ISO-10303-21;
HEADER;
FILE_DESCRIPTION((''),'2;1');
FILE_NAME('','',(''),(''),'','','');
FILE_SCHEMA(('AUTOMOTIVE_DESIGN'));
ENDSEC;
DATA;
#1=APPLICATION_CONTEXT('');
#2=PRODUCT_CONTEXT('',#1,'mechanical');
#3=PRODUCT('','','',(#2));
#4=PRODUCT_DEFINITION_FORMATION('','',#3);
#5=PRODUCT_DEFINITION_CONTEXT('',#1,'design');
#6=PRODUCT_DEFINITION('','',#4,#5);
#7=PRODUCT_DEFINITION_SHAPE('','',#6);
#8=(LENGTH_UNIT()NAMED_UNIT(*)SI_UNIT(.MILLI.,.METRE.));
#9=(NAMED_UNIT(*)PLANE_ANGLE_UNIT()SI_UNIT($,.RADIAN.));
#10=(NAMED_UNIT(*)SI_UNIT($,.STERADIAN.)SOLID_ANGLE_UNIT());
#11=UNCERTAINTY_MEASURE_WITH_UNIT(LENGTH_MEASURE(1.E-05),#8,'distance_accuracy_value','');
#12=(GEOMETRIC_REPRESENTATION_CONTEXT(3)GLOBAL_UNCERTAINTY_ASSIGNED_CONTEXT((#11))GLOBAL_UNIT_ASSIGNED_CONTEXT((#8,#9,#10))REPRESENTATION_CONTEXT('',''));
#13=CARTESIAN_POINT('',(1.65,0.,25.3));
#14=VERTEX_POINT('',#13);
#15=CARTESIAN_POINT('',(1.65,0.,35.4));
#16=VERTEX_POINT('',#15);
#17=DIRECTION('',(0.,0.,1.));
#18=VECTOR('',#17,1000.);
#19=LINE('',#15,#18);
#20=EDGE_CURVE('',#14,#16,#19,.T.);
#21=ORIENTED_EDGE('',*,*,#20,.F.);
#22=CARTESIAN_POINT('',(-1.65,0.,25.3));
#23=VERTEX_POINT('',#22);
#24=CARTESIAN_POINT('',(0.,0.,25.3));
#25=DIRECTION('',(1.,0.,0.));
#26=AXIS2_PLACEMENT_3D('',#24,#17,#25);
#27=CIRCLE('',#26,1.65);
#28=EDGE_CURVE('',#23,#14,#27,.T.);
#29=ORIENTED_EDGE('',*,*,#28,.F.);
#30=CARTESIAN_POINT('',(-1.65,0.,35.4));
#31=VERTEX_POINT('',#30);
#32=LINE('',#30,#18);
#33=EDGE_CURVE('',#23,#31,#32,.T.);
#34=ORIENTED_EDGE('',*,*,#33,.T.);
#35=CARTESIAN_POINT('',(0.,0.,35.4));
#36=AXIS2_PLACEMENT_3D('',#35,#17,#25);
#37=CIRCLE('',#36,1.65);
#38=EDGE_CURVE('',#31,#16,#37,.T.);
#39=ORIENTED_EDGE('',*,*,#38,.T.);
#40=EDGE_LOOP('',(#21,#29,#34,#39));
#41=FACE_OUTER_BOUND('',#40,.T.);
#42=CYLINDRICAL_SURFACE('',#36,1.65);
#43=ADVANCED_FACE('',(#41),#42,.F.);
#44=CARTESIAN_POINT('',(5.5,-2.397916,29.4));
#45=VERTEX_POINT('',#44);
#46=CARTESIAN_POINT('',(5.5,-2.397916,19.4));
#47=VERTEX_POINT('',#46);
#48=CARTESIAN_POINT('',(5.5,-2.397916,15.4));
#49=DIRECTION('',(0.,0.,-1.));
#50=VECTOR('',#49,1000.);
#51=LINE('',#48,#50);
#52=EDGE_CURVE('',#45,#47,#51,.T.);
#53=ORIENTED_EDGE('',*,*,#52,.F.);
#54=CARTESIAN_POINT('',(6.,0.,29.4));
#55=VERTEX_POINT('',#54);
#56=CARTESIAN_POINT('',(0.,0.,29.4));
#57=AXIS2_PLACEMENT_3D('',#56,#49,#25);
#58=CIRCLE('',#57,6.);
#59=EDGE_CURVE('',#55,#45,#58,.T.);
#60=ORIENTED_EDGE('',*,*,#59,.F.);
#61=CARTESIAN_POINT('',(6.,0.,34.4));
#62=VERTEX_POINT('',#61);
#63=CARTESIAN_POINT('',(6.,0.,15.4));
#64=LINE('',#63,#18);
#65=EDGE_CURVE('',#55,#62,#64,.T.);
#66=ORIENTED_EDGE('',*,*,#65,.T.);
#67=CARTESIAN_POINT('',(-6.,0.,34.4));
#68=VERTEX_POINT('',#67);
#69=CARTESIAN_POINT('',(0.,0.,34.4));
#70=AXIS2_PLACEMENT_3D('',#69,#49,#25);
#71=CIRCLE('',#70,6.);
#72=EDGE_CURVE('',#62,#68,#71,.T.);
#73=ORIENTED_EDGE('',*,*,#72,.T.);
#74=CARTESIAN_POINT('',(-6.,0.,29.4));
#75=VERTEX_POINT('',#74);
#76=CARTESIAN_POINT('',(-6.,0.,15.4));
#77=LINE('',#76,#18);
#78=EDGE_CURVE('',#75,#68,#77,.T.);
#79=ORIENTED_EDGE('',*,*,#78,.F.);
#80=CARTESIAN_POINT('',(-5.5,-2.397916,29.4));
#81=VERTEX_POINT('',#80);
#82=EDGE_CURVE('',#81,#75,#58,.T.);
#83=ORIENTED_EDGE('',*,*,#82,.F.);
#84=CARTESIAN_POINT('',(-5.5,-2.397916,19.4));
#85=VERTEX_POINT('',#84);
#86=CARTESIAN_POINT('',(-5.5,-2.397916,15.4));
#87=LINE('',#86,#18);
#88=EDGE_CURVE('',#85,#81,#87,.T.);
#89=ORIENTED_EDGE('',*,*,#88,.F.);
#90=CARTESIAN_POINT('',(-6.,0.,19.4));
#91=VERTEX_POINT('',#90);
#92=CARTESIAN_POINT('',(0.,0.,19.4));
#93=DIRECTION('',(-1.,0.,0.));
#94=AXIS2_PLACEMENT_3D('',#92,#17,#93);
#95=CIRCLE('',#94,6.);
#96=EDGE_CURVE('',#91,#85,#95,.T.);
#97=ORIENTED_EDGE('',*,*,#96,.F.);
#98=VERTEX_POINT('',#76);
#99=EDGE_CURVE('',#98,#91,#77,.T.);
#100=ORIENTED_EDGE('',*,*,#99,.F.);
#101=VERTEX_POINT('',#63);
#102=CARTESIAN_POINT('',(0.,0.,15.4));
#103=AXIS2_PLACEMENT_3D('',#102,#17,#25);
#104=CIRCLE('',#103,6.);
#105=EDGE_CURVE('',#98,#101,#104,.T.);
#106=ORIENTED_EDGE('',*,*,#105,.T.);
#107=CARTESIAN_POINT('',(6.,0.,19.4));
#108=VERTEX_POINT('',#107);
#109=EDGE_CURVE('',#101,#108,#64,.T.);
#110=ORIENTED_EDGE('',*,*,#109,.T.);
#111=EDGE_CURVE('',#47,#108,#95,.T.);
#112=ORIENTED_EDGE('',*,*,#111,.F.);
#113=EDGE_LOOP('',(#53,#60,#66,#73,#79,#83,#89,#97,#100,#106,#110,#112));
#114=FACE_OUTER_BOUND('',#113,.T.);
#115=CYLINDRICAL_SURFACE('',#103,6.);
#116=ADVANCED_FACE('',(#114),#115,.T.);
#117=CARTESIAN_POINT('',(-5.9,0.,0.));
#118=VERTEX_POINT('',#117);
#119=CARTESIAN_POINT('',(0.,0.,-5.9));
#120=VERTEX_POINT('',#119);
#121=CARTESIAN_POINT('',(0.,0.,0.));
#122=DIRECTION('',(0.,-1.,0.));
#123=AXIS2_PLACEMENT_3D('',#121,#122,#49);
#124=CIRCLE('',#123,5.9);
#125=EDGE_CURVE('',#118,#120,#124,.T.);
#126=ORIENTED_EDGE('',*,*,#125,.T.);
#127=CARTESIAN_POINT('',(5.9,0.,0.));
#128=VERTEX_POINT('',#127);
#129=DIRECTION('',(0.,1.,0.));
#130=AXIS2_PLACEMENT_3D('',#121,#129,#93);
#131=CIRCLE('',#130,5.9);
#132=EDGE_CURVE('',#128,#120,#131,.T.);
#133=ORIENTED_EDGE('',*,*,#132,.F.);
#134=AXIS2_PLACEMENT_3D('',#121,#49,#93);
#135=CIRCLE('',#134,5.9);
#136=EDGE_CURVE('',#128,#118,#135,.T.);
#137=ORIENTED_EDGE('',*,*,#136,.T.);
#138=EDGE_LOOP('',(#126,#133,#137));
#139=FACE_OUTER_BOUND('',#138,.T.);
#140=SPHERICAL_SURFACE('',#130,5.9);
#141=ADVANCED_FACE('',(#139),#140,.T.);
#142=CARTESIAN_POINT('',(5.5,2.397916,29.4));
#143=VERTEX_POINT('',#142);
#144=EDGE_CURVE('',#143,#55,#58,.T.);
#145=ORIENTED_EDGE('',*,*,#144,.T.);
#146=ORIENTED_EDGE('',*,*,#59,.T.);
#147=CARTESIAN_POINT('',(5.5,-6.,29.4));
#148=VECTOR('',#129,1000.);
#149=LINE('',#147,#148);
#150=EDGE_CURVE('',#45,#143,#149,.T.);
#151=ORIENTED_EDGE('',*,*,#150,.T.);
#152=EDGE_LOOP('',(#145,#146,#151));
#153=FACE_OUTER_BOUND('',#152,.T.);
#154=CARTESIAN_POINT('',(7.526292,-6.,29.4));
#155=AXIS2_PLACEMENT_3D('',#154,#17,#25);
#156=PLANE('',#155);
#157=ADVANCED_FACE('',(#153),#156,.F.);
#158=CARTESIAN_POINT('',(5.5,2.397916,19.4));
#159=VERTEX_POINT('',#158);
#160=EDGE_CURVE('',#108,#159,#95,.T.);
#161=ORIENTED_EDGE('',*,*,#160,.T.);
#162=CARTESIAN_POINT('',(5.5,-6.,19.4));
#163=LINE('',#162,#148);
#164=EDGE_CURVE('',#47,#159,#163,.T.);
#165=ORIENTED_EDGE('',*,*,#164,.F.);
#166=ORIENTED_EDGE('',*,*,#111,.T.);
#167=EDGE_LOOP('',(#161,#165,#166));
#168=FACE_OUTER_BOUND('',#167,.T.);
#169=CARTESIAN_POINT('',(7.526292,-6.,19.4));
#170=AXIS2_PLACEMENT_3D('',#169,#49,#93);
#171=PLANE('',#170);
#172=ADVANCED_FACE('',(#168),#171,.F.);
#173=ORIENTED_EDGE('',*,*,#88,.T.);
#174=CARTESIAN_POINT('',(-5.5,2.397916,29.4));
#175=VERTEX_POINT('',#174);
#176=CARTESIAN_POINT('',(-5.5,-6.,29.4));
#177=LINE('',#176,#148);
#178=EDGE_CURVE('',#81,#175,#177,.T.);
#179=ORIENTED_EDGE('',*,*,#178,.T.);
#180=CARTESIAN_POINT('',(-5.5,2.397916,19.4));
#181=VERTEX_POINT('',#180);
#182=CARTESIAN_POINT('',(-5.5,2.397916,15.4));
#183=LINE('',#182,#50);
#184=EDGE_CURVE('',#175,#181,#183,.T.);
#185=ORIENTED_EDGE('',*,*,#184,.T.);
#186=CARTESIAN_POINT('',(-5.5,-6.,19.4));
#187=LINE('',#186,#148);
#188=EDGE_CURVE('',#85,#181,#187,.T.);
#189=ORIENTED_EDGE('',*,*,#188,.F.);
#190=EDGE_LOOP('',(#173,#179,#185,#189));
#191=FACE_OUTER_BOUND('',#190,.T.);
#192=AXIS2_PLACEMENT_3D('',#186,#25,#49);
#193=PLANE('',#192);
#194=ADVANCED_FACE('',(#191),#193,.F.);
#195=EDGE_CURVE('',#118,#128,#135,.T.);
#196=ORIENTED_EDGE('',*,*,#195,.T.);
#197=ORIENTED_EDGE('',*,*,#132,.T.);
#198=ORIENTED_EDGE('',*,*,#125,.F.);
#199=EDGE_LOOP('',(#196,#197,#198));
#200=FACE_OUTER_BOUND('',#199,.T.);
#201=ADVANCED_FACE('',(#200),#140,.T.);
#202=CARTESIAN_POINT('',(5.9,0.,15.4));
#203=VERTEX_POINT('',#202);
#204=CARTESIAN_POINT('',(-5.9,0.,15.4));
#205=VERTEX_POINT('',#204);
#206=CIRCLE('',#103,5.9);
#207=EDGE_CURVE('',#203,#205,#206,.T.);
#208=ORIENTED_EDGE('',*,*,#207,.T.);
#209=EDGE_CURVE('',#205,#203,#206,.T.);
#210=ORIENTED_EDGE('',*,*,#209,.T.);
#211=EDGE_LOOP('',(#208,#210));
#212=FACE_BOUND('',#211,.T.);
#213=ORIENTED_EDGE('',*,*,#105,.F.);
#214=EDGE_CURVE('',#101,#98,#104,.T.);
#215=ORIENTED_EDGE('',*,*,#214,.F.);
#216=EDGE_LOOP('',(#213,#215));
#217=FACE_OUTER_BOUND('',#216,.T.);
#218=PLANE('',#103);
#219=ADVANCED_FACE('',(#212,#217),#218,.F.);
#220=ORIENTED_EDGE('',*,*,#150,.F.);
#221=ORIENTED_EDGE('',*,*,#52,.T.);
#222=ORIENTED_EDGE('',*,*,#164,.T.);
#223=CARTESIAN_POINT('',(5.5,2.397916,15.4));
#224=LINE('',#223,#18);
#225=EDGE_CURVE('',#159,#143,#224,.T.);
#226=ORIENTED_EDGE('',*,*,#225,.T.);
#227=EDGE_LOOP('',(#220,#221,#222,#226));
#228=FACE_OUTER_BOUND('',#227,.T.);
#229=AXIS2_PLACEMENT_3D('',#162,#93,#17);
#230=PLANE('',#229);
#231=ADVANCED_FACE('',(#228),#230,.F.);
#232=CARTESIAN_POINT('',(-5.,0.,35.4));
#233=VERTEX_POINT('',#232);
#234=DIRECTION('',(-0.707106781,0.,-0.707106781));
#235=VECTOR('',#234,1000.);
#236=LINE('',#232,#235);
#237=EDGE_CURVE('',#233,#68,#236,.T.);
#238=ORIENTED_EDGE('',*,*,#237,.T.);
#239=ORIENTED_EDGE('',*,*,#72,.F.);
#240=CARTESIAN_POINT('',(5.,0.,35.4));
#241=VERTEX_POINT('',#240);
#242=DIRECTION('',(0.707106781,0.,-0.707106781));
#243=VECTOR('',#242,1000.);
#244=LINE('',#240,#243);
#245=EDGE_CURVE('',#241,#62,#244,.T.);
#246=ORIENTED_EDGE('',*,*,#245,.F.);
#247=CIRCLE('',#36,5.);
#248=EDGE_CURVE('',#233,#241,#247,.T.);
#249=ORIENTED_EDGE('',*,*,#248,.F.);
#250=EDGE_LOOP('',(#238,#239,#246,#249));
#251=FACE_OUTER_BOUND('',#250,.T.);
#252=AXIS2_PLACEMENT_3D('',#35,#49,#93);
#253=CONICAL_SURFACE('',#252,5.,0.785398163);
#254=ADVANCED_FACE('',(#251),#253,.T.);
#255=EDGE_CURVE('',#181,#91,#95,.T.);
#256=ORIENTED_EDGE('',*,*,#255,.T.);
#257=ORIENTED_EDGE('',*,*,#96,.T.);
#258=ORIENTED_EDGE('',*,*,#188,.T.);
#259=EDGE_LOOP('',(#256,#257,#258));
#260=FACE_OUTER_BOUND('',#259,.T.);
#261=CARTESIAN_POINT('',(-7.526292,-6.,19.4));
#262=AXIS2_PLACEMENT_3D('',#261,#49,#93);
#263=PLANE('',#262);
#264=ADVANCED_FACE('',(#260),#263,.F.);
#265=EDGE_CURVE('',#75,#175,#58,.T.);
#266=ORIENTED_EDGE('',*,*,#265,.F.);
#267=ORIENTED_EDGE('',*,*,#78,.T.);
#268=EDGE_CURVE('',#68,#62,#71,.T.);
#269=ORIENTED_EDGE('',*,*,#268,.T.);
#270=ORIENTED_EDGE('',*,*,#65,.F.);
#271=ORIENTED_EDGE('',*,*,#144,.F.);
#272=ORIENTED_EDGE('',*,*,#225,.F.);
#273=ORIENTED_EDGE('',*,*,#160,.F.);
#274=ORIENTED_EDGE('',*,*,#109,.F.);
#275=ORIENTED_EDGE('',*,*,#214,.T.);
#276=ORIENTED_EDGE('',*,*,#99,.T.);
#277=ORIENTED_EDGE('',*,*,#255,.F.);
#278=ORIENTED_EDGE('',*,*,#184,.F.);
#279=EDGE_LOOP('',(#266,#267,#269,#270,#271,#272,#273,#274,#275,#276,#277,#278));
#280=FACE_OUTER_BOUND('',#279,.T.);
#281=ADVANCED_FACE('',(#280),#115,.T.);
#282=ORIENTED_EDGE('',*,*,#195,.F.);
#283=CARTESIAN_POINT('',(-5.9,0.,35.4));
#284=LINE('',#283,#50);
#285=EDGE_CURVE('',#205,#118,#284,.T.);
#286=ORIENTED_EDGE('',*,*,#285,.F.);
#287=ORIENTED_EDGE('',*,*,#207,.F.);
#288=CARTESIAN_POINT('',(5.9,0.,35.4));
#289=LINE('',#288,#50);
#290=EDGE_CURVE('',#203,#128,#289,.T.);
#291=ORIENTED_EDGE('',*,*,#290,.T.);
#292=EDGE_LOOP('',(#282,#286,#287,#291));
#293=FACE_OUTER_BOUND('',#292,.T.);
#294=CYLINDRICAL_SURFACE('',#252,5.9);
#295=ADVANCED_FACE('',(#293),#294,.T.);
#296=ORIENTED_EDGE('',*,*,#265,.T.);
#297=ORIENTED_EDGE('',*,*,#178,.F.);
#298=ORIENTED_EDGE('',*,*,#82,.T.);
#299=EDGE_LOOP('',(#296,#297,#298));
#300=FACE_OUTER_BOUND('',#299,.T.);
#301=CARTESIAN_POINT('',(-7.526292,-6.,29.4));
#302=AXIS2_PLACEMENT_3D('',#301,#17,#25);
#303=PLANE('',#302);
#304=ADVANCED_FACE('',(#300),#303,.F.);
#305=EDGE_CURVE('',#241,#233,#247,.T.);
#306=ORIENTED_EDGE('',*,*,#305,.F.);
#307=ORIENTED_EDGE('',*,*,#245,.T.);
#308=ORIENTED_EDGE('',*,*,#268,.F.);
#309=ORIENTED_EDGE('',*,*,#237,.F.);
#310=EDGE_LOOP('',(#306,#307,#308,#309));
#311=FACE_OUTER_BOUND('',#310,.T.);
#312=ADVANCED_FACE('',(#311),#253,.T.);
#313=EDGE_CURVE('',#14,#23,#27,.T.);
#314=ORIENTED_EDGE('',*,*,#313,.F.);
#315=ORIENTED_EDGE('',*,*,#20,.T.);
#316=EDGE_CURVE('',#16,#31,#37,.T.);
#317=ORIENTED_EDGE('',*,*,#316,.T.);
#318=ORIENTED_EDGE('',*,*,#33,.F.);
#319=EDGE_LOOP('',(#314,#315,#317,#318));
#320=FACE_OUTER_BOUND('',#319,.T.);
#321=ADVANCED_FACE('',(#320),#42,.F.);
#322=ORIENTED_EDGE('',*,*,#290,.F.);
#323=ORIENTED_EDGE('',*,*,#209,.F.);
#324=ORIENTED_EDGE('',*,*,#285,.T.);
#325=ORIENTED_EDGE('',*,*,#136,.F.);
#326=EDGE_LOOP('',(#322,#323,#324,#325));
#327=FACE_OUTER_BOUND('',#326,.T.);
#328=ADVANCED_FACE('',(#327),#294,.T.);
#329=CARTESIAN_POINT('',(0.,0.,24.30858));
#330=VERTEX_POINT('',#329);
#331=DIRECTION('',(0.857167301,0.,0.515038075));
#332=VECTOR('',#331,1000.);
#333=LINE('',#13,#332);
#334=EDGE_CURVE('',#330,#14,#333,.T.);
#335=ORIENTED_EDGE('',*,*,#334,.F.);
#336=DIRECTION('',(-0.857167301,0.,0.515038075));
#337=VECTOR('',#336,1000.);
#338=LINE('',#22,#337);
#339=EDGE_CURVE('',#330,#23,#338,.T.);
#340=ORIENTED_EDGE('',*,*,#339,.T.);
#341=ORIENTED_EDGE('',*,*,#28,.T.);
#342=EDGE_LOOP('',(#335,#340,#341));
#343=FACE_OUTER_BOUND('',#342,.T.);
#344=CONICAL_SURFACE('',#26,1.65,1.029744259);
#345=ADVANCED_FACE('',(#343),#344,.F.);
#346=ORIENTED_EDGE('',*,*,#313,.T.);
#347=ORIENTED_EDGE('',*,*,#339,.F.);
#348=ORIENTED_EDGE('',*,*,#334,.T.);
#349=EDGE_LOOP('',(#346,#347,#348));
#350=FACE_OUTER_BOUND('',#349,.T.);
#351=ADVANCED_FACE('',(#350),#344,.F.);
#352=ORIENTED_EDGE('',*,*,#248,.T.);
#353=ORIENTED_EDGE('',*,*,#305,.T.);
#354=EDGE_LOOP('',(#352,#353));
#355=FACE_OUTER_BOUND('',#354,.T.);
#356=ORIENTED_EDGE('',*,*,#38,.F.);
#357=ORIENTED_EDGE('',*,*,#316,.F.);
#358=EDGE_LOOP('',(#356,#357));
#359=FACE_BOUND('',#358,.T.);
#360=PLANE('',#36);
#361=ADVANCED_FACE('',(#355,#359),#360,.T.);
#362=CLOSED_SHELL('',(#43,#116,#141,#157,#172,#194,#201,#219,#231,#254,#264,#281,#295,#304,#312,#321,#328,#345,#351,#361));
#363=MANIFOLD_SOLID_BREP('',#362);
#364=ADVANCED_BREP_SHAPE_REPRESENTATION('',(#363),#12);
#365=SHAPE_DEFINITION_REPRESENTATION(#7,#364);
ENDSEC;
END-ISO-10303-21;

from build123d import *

# Parameters (mm, degrees)
SKETCH1_R               = 5.9
BOSS_EXTRUDE1_DEPTH     = 35.4
M4_TAPPED_HOLE1_D       = 3.3
M4_TAPPED_HOLE1_DEPTH   = 10.1
M4_TAPPED_HOLE1_TIP     = 0.991420021
SKETCH5_R               = 6
SKETCH5_R_2             = 4
BOSS_EXTRUDE2_DEPTH     = 20
CHAMFER1_SIZE           = 1
CUT_EXTRUDE1_DEPTH      = 37.402747149
CUT_EXTRUDE1_DEPTH_BACK = 37.402747149
SKETCH6_W               = 2.026292368
SKETCH6_H               = 10


with BuildPart() as part:
    # Sketch1 → Boss-Extrude1 (new body)
    with BuildSketch(Plane.XY):
        Circle(SKETCH1_R)
    extrude(amount=BOSS_EXTRUDE1_DEPTH)

    # Sketch2 → Revolve1 (revolve)
    with BuildSketch(Plane(origin=(0, 0, 0), x_dir=(1, 0, 0), z_dir=(0, 1, 0))):
        with BuildLine():
            Line((0, 5.9), (0, 0))
            Line((0, 0), (-5.9, 0))
            ThreePointArc((-5.9, 0), (-4.171930009, 4.171930009), (0, 5.9))
        make_face()
    revolve(axis=Axis((0, 0, -5.9), (0, 0, 1)))

    # M4 Tapped Hole1
    with Locations(Plane.XY.offset(35.4)):
        with Locations((0, 0)):
            Hole(M4_TAPPED_HOLE1_D / 2, depth=M4_TAPPED_HOLE1_DEPTH)
            with Locations((0, 0, -(M4_TAPPED_HOLE1_DEPTH + M4_TAPPED_HOLE1_TIP / 2))):  # 118° drill point
                Cone(0, M4_TAPPED_HOLE1_D / 2, M4_TAPPED_HOLE1_TIP, mode=Mode.SUBTRACT)

    # Sketch5 → Boss-Extrude2 (add)
    with BuildSketch(Plane.XY.offset(35.4)):
        Circle(SKETCH5_R)
        Circle(SKETCH5_R_2, mode=Mode.SUBTRACT)
    extrude(amount=-BOSS_EXTRUDE2_DEPTH)

    # Chamfer1
    chamfer1_edges = [part.edges().sort_by_distance(p)[0] for p in [
        (-6, 0, 35.4),
    ]]
    chamfer(chamfer1_edges, length=CHAMFER1_SIZE)

    # Sketch6 → Cut-Extrude1 (cut, two sides: drawn at the far end of the back side and taken through both)
    with BuildSketch(Plane(origin=(0, 0, 0), x_dir=(1, 0, 0), z_dir=(0, 1, 0)).offset(-CUT_EXTRUDE1_DEPTH_BACK)):
        with Locations((-6.513146184, -24.4)):
            Rectangle(SKETCH6_W, SKETCH6_H)
        with Locations((6.513146184, -24.4)):
            Rectangle(SKETCH6_W, SKETCH6_H)
    extrude(amount=CUT_EXTRUDE1_DEPTH + CUT_EXTRUDE1_DEPTH_BACK, mode=Mode.SUBTRACT)


solid = part.part
